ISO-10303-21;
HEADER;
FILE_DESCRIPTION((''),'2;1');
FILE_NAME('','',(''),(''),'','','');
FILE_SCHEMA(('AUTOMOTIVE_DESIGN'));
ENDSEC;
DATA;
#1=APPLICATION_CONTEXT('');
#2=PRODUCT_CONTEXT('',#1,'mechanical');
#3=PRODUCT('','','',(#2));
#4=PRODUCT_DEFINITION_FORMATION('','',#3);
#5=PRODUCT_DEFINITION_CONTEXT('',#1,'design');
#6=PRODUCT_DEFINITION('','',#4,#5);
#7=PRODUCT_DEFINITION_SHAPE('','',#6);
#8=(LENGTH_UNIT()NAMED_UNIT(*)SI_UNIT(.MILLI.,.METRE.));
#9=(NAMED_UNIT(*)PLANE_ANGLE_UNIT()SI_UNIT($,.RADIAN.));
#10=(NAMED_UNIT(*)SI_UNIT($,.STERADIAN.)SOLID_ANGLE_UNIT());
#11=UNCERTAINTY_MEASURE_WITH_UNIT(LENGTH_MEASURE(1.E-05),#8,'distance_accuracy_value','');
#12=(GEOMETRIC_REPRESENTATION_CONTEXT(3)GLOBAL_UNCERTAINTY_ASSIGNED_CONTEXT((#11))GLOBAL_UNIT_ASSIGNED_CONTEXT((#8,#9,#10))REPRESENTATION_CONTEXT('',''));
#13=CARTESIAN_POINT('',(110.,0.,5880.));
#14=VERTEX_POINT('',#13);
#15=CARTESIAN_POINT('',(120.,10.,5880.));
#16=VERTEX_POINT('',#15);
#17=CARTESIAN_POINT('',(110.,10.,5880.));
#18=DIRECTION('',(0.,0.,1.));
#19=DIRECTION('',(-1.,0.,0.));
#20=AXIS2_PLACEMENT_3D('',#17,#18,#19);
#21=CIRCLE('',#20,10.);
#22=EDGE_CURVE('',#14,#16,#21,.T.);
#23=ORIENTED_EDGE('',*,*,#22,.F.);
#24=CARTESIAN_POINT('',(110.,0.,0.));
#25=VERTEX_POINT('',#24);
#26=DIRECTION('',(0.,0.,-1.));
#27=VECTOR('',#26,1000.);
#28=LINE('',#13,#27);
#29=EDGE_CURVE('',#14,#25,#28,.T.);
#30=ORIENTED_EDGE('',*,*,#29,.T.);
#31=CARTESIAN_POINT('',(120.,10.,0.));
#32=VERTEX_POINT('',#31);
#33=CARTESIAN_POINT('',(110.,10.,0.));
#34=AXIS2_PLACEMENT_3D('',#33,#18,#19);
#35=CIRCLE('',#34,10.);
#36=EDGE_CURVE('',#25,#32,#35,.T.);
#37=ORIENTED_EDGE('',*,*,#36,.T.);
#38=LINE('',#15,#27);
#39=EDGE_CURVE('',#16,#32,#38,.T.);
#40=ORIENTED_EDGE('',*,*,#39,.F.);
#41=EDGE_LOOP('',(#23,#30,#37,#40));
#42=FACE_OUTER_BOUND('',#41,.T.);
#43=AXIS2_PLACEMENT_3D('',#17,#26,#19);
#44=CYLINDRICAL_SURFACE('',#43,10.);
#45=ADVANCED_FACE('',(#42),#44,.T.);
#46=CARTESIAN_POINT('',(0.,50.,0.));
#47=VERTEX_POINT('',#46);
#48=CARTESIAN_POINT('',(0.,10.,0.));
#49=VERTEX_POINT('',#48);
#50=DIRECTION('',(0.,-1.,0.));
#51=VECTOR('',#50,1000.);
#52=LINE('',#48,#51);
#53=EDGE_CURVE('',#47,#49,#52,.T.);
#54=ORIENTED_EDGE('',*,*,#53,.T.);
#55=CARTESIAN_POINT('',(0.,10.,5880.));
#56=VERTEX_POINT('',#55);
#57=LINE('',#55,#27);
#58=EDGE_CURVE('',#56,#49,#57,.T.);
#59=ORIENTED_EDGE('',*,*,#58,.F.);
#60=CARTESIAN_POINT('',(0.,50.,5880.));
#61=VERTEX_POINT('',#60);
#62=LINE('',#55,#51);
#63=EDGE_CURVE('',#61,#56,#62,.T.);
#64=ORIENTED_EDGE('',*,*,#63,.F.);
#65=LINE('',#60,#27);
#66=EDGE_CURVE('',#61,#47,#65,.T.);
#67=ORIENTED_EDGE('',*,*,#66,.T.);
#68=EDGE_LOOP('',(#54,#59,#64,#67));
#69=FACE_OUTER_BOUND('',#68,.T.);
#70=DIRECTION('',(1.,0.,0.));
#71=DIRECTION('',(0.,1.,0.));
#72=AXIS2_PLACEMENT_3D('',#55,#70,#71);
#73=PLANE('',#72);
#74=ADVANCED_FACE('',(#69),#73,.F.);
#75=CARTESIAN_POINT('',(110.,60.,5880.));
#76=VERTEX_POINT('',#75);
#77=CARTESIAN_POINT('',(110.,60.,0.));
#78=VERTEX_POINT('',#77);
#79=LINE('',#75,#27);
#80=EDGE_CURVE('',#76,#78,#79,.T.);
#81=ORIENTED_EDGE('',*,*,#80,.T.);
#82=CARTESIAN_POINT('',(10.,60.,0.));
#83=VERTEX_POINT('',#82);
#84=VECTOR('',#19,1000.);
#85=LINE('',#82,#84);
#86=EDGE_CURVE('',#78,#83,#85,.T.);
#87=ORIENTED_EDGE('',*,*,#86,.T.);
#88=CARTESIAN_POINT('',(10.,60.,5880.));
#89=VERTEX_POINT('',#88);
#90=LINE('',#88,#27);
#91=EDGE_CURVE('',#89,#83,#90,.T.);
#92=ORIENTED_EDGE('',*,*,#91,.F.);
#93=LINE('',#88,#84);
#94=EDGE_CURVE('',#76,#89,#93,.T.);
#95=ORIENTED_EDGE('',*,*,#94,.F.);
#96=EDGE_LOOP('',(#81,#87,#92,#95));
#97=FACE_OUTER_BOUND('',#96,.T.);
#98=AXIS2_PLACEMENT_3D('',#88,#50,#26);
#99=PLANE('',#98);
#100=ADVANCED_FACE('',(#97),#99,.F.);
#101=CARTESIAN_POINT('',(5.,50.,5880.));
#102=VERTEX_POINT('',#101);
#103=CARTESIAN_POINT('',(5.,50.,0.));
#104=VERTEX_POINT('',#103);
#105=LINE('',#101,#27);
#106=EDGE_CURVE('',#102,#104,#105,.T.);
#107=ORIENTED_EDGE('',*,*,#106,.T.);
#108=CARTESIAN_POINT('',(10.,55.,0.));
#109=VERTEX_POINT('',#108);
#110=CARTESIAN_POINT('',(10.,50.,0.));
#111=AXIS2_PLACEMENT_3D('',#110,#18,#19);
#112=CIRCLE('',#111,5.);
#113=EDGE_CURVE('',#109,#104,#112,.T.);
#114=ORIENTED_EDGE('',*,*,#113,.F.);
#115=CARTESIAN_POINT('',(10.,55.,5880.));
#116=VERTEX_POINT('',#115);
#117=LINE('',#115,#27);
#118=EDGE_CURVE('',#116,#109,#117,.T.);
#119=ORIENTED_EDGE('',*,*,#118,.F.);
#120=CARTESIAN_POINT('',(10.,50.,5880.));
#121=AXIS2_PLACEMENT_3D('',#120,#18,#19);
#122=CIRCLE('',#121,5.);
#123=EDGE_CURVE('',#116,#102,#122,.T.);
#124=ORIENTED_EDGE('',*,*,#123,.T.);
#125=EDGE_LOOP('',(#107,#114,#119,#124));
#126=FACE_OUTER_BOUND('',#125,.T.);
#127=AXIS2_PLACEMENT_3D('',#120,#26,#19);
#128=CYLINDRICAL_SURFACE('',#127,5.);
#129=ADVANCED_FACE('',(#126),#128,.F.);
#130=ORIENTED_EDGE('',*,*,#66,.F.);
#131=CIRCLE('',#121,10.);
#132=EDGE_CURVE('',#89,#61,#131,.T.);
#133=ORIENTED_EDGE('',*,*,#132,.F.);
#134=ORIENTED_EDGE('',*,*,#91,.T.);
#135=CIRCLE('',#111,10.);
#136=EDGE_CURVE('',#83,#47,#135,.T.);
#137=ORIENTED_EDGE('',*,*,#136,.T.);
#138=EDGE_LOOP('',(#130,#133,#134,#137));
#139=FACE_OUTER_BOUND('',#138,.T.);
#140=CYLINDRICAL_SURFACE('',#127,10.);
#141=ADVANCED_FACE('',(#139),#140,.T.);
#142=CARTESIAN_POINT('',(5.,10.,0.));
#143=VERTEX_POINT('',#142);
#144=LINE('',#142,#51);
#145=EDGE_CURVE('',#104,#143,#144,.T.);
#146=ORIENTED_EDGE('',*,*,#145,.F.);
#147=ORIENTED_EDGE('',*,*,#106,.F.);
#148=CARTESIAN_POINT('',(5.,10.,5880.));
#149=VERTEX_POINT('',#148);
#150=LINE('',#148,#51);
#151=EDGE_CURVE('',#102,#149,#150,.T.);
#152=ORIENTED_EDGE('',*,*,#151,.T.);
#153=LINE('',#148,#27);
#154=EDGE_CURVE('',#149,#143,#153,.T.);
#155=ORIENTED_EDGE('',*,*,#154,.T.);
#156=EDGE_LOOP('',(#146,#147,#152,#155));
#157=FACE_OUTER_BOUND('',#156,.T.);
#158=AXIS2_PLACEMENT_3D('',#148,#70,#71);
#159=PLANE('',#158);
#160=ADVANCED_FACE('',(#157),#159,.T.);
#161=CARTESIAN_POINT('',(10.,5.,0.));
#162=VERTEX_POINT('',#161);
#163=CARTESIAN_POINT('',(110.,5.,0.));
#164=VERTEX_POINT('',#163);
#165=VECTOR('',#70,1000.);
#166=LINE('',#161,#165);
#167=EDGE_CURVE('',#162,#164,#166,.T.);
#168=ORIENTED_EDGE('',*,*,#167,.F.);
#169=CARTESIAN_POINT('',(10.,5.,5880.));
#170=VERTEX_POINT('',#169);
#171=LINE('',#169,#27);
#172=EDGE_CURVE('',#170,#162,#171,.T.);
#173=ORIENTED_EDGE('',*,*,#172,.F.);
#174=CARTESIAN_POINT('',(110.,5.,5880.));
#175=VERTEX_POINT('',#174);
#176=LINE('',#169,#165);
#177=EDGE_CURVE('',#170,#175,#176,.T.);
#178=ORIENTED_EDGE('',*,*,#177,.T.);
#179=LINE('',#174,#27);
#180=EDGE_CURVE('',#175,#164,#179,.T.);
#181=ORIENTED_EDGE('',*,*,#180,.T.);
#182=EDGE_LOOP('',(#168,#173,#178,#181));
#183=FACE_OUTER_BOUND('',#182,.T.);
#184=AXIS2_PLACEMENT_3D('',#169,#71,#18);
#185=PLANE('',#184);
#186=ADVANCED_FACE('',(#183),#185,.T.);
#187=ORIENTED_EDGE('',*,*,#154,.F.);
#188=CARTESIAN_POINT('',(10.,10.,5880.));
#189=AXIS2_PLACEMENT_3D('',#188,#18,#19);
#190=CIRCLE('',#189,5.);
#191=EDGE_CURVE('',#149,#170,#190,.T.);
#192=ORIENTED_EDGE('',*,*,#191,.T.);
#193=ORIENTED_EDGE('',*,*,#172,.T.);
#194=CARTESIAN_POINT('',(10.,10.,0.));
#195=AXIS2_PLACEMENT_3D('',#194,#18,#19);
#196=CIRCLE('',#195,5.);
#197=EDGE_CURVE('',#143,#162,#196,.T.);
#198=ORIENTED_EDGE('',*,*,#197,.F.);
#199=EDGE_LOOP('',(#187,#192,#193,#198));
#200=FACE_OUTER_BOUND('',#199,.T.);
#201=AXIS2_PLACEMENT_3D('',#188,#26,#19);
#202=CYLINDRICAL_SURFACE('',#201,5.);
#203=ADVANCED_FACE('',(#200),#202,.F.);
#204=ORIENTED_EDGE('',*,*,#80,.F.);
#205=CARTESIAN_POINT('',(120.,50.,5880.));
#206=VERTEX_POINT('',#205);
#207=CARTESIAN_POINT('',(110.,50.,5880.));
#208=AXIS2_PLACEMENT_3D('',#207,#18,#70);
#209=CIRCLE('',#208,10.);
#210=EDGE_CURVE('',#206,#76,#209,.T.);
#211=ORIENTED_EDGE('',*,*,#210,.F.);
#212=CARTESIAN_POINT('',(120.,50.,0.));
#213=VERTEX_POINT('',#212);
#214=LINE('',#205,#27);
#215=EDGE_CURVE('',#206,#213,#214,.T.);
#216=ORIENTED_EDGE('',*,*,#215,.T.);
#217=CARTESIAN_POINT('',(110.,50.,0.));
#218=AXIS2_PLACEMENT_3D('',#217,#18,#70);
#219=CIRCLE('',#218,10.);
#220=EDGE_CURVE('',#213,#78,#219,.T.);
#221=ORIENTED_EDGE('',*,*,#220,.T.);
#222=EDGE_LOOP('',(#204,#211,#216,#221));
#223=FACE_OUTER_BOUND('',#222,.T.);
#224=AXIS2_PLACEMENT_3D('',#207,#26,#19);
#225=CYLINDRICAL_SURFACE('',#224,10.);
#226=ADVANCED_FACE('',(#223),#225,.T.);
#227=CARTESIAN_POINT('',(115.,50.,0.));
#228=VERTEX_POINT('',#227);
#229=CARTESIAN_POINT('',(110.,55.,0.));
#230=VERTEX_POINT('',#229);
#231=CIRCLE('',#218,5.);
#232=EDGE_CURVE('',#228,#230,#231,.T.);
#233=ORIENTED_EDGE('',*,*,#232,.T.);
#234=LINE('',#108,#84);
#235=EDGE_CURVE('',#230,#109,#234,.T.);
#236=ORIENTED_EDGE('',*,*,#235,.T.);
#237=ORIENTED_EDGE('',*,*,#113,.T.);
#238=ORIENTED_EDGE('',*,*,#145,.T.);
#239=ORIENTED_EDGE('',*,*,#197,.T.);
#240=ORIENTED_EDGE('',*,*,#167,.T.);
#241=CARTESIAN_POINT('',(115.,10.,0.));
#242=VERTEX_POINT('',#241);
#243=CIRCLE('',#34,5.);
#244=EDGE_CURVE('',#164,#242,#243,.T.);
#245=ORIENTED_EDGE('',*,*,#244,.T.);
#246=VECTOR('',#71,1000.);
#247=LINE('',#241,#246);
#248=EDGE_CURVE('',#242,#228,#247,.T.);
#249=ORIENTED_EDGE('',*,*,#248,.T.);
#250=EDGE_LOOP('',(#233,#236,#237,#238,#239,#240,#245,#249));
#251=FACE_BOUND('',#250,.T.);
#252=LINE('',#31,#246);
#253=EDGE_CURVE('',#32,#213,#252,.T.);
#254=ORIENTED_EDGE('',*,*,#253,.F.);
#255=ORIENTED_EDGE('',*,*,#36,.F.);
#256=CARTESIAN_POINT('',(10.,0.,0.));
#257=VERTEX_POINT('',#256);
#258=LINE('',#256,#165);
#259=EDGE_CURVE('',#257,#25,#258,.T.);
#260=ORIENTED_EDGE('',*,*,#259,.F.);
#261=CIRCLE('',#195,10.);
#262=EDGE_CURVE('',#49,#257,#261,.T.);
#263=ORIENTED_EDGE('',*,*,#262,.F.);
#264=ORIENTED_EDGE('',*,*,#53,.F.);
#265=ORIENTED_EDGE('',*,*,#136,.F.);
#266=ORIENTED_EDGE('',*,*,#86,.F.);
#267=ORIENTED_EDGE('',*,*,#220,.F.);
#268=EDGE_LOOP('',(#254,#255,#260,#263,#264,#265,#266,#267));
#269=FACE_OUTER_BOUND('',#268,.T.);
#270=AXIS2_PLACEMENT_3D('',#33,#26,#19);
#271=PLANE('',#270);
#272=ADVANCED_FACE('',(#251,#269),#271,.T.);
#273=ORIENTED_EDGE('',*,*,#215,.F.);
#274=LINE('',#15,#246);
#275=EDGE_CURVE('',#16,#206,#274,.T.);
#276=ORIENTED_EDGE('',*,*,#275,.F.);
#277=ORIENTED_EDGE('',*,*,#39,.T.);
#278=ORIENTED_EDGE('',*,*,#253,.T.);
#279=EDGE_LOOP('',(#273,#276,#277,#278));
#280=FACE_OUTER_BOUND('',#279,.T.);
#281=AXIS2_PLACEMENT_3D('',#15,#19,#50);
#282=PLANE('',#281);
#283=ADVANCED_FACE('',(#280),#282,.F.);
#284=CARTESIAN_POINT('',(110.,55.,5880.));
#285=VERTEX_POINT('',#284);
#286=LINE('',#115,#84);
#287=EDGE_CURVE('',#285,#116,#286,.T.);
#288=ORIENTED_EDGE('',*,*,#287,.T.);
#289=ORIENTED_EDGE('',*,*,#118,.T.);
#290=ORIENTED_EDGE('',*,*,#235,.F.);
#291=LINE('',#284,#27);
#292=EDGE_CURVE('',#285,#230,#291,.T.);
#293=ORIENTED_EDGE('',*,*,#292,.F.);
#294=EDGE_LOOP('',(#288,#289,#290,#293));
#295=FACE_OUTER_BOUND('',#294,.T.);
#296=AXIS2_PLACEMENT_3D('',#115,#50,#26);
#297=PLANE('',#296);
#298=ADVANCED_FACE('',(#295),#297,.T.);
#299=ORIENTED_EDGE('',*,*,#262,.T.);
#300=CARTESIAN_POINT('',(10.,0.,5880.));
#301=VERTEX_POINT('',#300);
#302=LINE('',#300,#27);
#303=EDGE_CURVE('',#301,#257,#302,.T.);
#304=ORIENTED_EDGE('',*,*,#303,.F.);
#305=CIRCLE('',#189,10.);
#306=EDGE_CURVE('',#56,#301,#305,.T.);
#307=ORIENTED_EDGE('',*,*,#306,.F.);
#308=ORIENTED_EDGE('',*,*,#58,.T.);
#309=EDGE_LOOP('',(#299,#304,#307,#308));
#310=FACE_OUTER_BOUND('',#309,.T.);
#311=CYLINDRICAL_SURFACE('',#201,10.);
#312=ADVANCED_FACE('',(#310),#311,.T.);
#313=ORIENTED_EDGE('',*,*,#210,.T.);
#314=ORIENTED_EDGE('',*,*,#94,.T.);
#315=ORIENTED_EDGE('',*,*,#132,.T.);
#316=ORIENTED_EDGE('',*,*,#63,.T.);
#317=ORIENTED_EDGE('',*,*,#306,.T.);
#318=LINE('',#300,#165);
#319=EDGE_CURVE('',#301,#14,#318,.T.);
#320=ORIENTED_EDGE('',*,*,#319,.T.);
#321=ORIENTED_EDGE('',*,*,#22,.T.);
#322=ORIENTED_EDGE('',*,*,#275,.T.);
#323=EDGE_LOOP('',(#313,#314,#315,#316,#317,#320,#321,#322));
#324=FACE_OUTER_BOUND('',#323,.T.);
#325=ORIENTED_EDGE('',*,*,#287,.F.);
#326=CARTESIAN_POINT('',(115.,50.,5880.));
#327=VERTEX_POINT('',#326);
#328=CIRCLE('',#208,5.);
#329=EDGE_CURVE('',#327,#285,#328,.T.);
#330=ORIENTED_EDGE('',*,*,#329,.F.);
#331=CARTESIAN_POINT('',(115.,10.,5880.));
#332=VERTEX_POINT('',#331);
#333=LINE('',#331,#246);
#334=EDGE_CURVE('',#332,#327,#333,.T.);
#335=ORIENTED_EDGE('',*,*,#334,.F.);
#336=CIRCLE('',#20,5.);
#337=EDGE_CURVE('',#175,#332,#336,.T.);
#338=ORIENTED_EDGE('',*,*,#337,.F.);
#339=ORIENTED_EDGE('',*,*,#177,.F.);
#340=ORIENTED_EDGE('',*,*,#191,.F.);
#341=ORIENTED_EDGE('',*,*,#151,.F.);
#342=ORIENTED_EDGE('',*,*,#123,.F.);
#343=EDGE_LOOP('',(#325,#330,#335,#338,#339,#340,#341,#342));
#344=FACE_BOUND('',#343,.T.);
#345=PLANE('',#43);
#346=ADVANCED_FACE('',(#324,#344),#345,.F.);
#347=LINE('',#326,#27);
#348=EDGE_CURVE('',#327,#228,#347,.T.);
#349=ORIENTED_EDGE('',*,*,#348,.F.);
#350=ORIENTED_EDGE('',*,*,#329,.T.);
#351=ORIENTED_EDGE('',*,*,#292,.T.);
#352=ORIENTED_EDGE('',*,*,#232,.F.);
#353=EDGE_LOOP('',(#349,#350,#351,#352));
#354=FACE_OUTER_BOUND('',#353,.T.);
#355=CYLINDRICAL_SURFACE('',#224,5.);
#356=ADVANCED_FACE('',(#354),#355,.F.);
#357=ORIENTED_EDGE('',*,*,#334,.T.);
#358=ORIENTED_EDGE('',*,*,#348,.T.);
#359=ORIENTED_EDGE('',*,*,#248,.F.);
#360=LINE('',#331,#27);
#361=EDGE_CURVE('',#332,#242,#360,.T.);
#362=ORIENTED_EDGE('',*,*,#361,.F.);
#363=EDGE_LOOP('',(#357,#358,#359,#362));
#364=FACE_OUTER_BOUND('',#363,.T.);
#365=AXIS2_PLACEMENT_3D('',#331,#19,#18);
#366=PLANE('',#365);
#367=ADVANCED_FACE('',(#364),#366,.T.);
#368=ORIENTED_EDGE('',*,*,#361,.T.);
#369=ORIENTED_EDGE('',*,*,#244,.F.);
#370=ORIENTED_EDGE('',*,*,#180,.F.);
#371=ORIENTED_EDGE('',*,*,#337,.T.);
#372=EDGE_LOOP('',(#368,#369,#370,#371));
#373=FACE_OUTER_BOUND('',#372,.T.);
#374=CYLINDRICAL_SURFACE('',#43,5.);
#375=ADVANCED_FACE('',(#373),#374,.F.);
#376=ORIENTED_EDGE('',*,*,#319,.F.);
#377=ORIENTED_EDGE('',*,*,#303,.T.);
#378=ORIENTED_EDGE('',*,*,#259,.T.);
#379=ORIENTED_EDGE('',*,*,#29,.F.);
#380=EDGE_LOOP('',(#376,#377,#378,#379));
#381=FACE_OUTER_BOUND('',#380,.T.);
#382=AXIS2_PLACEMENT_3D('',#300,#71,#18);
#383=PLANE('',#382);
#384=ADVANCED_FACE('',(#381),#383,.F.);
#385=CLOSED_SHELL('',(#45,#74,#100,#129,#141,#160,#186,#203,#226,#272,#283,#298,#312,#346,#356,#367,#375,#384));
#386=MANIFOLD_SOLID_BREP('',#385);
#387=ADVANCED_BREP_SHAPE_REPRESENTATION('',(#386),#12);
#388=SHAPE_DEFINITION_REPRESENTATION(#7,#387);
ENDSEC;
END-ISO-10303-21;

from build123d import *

# Parameters (mm, degrees)
BOSS_EXTRUDE1_DEPTH = 5880


with BuildPart() as part:
    # Sketch1 → Boss-Extrude1 (new body)
    with BuildSketch(Plane.XY):
        with BuildLine():
            Line((10, 0), (110, 0))
            ThreePointArc((110, 0), (117.071067812, 2.928932188), (120, 10))
            Line((120, 10), (120, 50))
            ThreePointArc((120, 50), (117.071067812, 57.071067812), (110, 60))
            Line((110, 60), (10, 60))
            ThreePointArc((10, 60), (2.928932188, 57.071067812), (0, 50))
            Line((0, 50), (0, 10))
            ThreePointArc((0, 10), (2.928932188, 2.928932188), (10, 0))
        make_face()
        with BuildLine():
            Line((10, 55), (110, 55))
            ThreePointArc((110, 55), (113.535533906, 53.535533906), (115, 50))
            Line((115, 50), (115, 10))
            ThreePointArc((115, 10), (113.535533906, 6.464466094), (110, 5))
            Line((110, 5), (10, 5))
            ThreePointArc((10, 5), (6.464466094, 6.464466094), (5, 10))
            Line((5, 10), (5, 50))
            ThreePointArc((5, 50), (6.464466094, 53.535533906), (10, 55))
        make_face(mode=Mode.SUBTRACT)
    extrude(amount=BOSS_EXTRUDE1_DEPTH)


solid = part.part
